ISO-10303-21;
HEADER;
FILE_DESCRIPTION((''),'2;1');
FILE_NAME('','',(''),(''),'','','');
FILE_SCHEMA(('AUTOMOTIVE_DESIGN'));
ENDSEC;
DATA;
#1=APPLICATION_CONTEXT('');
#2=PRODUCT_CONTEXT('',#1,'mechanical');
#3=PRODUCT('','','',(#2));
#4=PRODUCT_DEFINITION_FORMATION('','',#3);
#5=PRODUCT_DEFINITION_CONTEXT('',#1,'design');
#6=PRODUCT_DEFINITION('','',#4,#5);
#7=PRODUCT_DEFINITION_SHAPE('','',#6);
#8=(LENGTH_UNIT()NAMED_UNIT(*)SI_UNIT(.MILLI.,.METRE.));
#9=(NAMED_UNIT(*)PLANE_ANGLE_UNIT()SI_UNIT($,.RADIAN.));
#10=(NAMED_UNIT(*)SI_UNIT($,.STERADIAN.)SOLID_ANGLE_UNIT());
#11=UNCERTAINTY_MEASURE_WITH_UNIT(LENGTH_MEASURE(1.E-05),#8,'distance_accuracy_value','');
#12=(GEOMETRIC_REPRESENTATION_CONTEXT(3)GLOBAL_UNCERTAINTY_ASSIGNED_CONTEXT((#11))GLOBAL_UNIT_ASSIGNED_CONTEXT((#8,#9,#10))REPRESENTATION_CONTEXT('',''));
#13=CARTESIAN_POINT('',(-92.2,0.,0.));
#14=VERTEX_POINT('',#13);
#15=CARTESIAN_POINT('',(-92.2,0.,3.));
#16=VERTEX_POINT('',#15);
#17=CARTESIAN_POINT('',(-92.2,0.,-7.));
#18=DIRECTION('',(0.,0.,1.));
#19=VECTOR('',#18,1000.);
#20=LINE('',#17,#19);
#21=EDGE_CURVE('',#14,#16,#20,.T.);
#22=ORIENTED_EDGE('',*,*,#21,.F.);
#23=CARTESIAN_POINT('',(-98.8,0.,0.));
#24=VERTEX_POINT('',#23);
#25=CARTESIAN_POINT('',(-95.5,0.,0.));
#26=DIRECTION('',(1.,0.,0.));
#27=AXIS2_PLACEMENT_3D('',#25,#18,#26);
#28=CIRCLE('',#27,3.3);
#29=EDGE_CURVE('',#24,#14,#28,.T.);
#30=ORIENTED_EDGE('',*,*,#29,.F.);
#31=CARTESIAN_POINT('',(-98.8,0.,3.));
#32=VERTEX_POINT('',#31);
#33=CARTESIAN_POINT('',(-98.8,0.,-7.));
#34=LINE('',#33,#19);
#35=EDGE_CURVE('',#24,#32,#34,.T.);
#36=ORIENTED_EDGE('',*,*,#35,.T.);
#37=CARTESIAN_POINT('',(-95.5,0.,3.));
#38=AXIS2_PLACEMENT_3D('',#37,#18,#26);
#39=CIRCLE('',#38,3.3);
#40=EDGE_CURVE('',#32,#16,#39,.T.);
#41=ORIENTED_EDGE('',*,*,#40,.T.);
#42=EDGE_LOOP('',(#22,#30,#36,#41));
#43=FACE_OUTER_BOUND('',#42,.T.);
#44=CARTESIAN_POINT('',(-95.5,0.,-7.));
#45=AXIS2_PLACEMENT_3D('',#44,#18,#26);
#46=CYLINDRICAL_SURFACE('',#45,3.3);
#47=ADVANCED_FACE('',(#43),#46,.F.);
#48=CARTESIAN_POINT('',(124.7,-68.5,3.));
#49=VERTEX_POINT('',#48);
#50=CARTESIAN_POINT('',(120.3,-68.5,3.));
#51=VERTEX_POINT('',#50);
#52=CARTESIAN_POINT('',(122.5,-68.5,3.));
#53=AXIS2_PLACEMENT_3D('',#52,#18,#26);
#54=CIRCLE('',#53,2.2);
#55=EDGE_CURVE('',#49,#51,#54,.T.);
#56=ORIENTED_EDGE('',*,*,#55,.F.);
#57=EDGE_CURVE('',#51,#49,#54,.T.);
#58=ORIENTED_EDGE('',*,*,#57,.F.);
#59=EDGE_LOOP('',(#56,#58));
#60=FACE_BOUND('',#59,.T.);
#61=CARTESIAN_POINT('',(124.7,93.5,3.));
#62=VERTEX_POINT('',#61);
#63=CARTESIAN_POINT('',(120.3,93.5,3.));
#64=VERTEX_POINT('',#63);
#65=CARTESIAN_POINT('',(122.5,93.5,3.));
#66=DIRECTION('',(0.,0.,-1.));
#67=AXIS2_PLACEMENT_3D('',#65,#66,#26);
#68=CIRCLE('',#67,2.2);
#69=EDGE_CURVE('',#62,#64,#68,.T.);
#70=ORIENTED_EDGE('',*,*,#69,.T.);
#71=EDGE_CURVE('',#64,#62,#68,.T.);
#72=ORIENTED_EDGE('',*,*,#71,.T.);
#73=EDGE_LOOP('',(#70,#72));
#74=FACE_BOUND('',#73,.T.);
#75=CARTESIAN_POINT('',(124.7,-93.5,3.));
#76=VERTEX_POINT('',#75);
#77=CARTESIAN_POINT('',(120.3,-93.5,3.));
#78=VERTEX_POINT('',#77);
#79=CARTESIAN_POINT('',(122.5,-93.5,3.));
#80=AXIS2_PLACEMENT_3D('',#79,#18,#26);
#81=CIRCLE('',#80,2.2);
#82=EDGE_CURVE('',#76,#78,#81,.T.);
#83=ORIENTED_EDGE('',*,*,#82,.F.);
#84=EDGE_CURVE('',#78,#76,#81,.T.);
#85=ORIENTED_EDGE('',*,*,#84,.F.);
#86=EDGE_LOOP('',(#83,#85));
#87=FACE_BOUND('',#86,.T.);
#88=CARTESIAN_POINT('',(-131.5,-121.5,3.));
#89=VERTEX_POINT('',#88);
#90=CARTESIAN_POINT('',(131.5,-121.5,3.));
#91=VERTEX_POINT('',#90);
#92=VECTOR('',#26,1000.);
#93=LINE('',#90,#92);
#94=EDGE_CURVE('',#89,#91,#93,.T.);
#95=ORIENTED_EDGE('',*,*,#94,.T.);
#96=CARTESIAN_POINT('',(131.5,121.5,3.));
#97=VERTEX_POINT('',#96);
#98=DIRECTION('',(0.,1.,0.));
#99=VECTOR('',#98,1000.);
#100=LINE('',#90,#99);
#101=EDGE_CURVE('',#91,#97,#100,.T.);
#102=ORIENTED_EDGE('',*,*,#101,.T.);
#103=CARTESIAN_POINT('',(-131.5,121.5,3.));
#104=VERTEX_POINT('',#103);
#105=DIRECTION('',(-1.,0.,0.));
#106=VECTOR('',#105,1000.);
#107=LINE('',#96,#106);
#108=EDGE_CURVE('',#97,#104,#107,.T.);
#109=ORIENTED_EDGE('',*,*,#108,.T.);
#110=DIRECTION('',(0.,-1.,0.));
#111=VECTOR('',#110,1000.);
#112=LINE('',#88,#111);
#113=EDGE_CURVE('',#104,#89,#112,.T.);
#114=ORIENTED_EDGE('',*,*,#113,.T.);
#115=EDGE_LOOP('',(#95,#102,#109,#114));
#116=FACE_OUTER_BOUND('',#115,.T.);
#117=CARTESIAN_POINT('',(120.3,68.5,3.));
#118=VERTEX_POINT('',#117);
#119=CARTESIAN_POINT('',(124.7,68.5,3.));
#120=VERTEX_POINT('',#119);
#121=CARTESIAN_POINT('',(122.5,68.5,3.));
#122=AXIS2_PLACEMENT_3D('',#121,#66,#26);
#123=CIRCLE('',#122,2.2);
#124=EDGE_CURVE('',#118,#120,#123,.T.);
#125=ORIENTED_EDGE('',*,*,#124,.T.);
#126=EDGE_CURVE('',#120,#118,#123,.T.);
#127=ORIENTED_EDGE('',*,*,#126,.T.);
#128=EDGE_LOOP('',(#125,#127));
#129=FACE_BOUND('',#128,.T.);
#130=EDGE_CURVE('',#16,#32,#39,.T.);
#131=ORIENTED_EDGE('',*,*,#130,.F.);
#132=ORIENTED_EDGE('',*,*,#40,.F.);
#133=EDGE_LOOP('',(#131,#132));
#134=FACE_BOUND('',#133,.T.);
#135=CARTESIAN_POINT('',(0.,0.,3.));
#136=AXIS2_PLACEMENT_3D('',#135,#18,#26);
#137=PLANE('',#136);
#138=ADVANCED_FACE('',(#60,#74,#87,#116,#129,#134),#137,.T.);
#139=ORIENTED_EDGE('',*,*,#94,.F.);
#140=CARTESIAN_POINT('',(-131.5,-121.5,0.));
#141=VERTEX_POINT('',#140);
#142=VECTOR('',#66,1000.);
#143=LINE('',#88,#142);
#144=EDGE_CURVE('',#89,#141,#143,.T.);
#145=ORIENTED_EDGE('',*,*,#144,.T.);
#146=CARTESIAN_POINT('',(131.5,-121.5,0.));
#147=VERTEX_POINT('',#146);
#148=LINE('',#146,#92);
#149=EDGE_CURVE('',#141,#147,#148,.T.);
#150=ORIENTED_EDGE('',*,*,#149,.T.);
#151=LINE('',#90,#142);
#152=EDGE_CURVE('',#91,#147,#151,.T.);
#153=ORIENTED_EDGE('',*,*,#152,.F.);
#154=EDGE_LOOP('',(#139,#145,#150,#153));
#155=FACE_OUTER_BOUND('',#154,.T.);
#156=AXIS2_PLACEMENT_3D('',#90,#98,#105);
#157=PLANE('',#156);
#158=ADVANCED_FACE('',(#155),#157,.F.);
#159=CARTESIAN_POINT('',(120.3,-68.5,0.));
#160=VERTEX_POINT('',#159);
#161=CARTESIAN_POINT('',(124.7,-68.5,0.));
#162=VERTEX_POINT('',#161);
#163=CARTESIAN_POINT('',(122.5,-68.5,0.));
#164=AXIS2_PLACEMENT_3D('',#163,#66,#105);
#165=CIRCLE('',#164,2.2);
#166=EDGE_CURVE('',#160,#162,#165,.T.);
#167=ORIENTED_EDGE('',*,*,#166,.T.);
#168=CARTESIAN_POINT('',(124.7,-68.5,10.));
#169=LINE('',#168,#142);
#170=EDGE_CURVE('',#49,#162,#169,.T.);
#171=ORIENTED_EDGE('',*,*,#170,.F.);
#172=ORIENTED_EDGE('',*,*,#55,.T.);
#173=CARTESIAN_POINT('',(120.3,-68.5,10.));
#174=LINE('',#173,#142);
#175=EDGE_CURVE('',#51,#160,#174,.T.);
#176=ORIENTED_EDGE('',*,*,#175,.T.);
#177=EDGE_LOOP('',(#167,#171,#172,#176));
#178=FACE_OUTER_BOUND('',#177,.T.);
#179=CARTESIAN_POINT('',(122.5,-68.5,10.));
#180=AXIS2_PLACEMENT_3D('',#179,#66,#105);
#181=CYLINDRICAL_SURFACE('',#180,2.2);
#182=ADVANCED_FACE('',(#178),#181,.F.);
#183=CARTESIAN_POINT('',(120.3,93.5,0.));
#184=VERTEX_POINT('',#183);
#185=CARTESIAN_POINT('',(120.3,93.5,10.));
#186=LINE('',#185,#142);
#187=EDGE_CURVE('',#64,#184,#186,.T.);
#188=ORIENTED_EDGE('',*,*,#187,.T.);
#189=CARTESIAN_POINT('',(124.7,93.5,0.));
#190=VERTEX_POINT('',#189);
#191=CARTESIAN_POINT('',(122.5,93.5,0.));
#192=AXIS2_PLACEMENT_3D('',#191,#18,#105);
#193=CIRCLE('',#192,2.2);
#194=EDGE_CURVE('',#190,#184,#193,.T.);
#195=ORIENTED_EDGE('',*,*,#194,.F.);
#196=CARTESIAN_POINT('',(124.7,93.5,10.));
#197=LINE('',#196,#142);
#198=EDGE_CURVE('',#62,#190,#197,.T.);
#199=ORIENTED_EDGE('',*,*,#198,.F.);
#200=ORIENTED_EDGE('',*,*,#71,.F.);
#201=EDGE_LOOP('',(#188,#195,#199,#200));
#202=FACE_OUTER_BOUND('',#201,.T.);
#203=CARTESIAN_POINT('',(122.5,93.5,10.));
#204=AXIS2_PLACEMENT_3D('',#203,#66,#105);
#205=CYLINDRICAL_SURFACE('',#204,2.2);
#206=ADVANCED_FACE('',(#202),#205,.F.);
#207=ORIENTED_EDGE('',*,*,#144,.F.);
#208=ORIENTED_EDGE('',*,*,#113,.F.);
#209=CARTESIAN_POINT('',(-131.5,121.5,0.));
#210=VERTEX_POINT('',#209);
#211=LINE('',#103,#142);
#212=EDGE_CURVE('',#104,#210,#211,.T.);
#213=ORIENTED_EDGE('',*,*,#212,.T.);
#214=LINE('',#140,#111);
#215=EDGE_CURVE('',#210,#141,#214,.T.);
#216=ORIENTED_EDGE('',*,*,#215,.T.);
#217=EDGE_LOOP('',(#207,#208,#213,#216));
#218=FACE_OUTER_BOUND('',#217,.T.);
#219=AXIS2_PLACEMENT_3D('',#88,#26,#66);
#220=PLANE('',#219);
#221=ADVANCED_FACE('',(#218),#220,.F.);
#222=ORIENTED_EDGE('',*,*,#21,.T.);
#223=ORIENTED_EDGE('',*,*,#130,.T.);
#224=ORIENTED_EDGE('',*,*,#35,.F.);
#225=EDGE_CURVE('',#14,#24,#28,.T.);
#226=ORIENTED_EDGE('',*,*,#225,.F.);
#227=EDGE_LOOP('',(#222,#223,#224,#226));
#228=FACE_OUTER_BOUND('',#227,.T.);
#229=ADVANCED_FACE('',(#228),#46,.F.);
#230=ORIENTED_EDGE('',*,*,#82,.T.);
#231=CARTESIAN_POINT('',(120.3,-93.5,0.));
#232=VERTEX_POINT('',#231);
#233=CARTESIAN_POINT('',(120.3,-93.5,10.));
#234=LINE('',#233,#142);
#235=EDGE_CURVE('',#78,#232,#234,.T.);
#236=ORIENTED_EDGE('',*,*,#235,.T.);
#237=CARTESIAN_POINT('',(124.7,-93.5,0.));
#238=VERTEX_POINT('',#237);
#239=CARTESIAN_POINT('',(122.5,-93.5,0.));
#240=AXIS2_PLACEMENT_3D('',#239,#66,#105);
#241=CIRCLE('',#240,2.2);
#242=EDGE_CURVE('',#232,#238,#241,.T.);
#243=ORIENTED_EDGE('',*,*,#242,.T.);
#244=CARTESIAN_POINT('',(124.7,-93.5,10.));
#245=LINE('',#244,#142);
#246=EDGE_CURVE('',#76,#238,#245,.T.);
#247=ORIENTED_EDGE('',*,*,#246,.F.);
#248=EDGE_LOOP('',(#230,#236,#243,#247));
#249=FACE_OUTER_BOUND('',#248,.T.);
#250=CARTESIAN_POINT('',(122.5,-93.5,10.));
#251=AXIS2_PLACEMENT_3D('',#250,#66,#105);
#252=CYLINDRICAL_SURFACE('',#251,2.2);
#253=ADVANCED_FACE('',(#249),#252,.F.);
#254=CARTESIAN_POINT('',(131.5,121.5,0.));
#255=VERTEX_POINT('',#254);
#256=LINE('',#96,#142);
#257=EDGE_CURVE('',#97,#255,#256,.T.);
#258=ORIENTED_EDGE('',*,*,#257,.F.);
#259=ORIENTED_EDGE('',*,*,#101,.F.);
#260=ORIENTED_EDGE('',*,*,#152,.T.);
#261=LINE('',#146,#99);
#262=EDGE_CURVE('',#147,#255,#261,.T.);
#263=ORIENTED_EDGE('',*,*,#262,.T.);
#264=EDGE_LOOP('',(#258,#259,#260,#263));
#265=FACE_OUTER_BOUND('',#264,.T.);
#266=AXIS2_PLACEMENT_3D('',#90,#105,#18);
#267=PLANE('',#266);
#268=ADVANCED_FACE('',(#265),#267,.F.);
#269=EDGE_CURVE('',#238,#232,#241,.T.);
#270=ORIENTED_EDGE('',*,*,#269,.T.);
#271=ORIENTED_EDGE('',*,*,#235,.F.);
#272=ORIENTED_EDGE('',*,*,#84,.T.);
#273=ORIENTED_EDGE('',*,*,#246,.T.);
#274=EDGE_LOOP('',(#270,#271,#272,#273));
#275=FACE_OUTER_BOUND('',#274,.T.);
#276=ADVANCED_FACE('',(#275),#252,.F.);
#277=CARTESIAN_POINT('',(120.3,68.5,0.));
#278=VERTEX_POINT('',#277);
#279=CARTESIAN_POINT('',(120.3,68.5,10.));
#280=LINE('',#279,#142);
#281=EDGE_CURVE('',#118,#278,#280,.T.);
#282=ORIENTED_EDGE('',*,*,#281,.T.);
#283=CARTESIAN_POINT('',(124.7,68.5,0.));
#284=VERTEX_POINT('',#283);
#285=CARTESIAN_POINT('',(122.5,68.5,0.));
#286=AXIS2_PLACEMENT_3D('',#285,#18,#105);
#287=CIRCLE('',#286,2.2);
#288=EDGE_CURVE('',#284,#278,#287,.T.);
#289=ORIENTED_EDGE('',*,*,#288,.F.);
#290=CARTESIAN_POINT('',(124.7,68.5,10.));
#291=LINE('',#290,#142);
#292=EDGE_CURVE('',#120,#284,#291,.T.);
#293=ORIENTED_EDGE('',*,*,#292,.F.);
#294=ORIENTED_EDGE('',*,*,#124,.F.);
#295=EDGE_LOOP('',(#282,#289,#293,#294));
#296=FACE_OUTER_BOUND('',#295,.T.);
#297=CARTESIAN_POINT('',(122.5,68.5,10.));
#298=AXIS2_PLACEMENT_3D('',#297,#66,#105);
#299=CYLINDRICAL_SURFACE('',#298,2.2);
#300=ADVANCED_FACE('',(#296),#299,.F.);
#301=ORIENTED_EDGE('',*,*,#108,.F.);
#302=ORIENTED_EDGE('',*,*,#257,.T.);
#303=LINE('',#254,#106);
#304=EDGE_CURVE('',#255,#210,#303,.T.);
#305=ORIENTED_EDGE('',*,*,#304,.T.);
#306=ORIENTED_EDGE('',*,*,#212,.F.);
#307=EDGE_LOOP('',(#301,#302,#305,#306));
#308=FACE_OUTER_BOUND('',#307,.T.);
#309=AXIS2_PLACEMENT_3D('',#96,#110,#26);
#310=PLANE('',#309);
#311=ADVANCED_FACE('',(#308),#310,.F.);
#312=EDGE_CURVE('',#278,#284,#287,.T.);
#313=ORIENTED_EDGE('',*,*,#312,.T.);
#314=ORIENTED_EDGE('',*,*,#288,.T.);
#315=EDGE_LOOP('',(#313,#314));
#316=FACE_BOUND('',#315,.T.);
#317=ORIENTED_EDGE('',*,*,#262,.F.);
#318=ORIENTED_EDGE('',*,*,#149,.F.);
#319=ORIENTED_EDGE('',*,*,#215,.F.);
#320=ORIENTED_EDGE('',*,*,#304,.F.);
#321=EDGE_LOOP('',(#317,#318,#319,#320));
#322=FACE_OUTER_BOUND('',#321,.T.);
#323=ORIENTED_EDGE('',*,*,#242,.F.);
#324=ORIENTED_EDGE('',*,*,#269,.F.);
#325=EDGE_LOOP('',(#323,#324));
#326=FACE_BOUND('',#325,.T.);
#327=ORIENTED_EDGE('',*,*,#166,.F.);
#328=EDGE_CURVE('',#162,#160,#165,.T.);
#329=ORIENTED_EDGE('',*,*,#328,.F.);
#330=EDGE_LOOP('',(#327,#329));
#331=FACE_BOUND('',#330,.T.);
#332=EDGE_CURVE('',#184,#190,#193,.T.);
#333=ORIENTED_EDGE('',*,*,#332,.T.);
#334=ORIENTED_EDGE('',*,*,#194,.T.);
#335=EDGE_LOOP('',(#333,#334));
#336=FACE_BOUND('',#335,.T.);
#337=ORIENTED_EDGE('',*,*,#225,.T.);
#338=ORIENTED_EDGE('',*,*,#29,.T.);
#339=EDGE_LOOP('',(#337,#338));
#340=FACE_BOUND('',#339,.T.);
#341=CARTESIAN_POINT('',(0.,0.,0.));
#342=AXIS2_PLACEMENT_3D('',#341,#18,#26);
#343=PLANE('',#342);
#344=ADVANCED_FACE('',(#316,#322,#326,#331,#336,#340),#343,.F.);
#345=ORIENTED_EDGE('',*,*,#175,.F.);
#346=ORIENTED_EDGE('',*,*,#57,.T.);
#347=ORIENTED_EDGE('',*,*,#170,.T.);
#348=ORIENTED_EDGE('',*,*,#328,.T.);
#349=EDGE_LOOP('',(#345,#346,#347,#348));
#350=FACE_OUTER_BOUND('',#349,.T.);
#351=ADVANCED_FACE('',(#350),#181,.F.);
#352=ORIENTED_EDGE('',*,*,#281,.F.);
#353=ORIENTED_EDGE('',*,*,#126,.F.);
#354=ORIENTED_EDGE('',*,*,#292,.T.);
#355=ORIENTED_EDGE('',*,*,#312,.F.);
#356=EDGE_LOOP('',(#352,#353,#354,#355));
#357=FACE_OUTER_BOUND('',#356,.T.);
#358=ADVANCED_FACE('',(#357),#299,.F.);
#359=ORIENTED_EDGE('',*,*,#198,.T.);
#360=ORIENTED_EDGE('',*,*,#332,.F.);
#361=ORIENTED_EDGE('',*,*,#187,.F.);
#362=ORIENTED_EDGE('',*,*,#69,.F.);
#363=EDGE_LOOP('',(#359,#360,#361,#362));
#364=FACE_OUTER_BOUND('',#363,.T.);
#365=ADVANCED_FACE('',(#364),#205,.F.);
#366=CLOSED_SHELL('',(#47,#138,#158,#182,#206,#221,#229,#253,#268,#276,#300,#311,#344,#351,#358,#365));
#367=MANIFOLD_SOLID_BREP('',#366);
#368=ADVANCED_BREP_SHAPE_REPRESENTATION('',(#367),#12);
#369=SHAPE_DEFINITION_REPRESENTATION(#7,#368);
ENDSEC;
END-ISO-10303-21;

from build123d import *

# Parameters (mm, degrees)
SKETCH_1_W          = 263
SKETCH_1_H          = 243
EXTRUDE_1_DEPTH     = 3
SKETCH_4_R          = 2.2
CUT_EXTRUDE_2_DEPTH = 10
SKETCH_5_R          = 3.3
CUT_EXTRUDE_3_DEPTH = 10


with BuildPart() as part:
    # 草图1 → 凸台-拉伸1 (new body)
    with BuildSketch(Plane.XY):
        Rectangle(SKETCH_1_W, SKETCH_1_H)
    extrude(amount=EXTRUDE_1_DEPTH)

    # 草图4 → 切除-拉伸2 (cut)
    with BuildSketch(Plane(origin=(0, 0, 0), x_dir=(-1, 0, 0), z_dir=(0, 0, -1))):
        with Locations((-122.5, -68.5)):
            Circle(SKETCH_4_R)
        with Locations((-122.5, -93.5)):
            Circle(SKETCH_4_R)
    cut_extrude_2 = extrude(amount=-CUT_EXTRUDE_2_DEPTH, mode=Mode.SUBTRACT)

    # 镜向1: 切除-拉伸2 across plane
    add(cut_extrude_2.mirror(Plane.ZX), mode=Mode.SUBTRACT)

    # 草图5 → 切除-拉伸3 (cut)
    with BuildSketch(Plane.XY.offset(3)):
        with Locations((-95.5, 0)):
            Circle(SKETCH_5_R)
    extrude(amount=-CUT_EXTRUDE_3_DEPTH, mode=Mode.SUBTRACT)


solid = part.part
